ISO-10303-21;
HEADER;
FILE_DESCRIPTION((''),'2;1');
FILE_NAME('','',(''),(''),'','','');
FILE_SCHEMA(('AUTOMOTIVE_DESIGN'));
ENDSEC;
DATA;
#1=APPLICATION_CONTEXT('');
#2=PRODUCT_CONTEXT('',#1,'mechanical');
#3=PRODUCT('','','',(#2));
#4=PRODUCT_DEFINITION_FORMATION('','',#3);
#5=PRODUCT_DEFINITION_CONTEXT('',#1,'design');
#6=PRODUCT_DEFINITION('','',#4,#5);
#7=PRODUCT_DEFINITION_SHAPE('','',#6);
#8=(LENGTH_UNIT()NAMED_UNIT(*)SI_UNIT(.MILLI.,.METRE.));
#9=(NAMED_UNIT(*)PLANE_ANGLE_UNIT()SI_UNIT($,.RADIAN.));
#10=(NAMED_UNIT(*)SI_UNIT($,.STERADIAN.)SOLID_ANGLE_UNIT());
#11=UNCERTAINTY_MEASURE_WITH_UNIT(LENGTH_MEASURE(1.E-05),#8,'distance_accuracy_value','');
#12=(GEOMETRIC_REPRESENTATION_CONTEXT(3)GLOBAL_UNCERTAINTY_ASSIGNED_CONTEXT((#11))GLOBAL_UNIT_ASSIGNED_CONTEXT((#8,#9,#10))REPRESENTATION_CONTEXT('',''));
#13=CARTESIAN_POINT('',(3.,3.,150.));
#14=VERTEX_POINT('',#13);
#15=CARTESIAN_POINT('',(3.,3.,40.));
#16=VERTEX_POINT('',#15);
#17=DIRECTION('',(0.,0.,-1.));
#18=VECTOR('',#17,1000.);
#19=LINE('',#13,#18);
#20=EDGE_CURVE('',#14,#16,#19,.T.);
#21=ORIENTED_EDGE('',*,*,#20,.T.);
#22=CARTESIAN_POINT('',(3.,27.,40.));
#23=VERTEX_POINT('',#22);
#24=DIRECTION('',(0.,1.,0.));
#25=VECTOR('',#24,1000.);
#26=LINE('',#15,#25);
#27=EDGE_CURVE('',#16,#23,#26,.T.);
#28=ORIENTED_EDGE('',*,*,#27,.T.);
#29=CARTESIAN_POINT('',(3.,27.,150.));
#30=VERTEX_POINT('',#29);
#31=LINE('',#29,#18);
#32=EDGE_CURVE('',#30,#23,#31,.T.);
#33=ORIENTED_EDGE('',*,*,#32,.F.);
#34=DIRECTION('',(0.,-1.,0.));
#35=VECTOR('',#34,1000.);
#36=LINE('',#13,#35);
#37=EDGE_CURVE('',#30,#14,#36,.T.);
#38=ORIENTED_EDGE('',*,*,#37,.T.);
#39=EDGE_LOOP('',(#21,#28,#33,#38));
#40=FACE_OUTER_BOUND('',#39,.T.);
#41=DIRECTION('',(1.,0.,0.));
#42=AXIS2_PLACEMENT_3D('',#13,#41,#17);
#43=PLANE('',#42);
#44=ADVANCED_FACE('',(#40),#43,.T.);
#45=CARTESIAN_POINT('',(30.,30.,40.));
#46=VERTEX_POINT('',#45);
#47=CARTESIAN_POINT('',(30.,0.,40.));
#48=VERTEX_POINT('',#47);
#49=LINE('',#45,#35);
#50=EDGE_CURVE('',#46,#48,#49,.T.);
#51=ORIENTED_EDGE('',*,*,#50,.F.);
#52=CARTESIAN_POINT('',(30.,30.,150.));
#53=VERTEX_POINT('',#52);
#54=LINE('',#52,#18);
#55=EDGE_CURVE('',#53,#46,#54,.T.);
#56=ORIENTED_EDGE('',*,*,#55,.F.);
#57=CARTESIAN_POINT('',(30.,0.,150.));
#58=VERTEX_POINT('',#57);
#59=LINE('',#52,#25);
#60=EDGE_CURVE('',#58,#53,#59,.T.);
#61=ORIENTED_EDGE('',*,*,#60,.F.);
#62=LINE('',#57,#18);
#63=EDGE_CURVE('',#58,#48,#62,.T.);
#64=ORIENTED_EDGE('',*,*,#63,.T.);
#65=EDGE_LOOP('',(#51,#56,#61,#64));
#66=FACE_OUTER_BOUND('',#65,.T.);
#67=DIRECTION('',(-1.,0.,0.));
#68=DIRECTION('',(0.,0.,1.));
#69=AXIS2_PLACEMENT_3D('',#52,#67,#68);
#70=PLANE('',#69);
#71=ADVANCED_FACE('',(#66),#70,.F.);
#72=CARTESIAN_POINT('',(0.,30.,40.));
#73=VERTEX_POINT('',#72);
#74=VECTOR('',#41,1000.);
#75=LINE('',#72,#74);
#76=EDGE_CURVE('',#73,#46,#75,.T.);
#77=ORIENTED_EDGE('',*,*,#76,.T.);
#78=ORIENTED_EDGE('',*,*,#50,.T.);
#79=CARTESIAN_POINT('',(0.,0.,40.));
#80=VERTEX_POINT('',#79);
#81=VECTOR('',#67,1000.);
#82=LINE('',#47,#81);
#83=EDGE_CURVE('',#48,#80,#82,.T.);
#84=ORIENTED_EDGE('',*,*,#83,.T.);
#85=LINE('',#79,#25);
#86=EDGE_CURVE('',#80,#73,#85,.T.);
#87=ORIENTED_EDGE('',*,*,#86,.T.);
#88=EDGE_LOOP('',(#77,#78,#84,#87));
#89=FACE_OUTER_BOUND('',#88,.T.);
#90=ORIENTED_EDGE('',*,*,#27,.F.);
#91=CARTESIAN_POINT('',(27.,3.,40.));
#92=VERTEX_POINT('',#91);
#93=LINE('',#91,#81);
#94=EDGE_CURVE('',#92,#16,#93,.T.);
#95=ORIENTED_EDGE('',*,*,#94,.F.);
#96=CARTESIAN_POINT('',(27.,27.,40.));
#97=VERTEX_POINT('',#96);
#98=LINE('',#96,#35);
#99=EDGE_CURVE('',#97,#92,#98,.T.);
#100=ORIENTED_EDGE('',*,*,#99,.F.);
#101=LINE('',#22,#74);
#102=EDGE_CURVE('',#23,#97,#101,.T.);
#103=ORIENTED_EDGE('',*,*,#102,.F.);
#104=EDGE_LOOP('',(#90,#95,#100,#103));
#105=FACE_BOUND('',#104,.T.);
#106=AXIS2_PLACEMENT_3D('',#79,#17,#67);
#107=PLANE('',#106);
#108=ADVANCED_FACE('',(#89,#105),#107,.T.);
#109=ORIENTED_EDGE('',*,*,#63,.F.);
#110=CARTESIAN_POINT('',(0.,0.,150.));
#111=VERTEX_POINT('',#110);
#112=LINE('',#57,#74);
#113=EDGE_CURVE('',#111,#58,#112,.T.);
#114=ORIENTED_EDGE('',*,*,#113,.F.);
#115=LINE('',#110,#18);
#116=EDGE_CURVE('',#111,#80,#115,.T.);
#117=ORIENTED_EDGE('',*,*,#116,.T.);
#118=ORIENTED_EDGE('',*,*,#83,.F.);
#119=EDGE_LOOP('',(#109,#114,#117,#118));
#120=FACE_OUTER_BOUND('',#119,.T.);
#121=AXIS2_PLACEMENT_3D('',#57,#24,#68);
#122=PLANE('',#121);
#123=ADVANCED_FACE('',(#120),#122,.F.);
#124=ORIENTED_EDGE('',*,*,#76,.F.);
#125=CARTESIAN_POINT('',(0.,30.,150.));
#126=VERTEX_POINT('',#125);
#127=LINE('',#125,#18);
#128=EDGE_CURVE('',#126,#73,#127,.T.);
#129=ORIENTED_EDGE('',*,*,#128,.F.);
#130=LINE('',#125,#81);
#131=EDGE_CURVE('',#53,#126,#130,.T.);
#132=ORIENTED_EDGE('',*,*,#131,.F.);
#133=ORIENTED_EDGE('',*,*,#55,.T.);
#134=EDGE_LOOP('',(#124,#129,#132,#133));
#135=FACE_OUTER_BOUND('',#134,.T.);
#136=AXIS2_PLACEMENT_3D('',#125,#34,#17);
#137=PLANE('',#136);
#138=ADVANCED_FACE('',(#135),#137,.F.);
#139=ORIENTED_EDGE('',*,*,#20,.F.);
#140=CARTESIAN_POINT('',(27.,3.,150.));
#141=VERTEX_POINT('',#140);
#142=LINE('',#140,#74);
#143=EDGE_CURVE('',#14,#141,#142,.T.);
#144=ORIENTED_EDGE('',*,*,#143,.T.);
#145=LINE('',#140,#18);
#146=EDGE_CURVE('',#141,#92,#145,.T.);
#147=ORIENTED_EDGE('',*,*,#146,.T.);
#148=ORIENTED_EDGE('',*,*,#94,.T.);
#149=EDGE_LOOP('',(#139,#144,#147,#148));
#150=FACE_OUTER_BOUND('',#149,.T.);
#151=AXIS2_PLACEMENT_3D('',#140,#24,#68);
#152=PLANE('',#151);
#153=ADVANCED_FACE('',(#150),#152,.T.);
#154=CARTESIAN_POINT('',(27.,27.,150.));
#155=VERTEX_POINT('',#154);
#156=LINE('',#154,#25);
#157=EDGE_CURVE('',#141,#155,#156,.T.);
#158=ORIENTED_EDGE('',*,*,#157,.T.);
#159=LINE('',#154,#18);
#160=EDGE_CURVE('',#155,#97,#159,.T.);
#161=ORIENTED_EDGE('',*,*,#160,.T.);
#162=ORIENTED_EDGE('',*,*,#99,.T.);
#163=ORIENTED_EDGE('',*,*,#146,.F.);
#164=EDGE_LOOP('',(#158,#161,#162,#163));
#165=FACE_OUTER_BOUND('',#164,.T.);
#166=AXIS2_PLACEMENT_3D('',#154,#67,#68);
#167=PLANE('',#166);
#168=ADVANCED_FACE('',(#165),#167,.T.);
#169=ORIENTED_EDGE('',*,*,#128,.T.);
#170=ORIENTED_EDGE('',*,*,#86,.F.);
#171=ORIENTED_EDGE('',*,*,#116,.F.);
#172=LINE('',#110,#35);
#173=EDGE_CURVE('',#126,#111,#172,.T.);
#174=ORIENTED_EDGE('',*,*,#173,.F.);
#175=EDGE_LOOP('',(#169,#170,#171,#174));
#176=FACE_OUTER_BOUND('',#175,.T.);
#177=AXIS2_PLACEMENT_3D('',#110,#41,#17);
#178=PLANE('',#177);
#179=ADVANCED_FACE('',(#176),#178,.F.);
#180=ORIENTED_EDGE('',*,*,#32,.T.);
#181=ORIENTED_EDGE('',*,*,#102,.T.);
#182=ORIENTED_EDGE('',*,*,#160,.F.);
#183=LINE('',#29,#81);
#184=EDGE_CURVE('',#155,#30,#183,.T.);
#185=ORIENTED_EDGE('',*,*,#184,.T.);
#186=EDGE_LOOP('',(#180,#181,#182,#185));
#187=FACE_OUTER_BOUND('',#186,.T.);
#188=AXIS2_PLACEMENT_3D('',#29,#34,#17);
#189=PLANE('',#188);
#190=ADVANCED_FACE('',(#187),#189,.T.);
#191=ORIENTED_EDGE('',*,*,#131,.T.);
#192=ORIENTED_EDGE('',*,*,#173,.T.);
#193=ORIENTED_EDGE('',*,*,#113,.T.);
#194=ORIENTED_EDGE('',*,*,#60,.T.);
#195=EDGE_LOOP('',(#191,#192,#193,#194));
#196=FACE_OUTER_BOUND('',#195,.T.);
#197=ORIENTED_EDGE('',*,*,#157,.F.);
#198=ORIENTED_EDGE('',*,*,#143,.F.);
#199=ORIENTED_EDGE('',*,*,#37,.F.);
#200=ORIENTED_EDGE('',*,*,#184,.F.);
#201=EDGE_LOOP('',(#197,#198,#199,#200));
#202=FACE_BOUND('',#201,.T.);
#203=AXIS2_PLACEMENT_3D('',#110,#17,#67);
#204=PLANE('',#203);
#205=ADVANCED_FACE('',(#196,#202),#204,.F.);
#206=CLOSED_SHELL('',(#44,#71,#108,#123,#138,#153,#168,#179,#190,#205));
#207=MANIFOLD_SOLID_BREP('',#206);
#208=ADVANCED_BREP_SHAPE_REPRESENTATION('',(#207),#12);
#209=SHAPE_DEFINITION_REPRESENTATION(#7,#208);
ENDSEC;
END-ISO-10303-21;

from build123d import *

# Parameters (mm, degrees)
SKETCH_1_W          = 30
SKETCH_1_H          = 30
SKETCH_1_W_2        = 24
SKETCH_1_H_2        = 24
EXTRUDE_1_DEPTH     = 150
SKETCH_2_W          = 30
SKETCH_2_H          = 30
CUT_EXTRUDE_1_DEPTH = 40


with BuildPart() as part:
    # 草图1 → 凸台-拉伸1 (new body)
    with BuildSketch(Plane.XY):
        with Locations((15, 15)):
            Rectangle(SKETCH_1_W, SKETCH_1_H)
        with Locations((15, 15)):
            Rectangle(SKETCH_1_W_2, SKETCH_1_H_2, mode=Mode.SUBTRACT)
    extrude(amount=EXTRUDE_1_DEPTH)

    # 草图2 → 切除-拉伸1 (cut)
    with BuildSketch(Plane(origin=(0, 0, 0), x_dir=(-1, 0, 0), z_dir=(0, 0, -1))):
        with Locations((-15, 15)):
            Rectangle(SKETCH_2_W, SKETCH_2_H)
    extrude(amount=-CUT_EXTRUDE_1_DEPTH, mode=Mode.SUBTRACT)


solid = part.part
